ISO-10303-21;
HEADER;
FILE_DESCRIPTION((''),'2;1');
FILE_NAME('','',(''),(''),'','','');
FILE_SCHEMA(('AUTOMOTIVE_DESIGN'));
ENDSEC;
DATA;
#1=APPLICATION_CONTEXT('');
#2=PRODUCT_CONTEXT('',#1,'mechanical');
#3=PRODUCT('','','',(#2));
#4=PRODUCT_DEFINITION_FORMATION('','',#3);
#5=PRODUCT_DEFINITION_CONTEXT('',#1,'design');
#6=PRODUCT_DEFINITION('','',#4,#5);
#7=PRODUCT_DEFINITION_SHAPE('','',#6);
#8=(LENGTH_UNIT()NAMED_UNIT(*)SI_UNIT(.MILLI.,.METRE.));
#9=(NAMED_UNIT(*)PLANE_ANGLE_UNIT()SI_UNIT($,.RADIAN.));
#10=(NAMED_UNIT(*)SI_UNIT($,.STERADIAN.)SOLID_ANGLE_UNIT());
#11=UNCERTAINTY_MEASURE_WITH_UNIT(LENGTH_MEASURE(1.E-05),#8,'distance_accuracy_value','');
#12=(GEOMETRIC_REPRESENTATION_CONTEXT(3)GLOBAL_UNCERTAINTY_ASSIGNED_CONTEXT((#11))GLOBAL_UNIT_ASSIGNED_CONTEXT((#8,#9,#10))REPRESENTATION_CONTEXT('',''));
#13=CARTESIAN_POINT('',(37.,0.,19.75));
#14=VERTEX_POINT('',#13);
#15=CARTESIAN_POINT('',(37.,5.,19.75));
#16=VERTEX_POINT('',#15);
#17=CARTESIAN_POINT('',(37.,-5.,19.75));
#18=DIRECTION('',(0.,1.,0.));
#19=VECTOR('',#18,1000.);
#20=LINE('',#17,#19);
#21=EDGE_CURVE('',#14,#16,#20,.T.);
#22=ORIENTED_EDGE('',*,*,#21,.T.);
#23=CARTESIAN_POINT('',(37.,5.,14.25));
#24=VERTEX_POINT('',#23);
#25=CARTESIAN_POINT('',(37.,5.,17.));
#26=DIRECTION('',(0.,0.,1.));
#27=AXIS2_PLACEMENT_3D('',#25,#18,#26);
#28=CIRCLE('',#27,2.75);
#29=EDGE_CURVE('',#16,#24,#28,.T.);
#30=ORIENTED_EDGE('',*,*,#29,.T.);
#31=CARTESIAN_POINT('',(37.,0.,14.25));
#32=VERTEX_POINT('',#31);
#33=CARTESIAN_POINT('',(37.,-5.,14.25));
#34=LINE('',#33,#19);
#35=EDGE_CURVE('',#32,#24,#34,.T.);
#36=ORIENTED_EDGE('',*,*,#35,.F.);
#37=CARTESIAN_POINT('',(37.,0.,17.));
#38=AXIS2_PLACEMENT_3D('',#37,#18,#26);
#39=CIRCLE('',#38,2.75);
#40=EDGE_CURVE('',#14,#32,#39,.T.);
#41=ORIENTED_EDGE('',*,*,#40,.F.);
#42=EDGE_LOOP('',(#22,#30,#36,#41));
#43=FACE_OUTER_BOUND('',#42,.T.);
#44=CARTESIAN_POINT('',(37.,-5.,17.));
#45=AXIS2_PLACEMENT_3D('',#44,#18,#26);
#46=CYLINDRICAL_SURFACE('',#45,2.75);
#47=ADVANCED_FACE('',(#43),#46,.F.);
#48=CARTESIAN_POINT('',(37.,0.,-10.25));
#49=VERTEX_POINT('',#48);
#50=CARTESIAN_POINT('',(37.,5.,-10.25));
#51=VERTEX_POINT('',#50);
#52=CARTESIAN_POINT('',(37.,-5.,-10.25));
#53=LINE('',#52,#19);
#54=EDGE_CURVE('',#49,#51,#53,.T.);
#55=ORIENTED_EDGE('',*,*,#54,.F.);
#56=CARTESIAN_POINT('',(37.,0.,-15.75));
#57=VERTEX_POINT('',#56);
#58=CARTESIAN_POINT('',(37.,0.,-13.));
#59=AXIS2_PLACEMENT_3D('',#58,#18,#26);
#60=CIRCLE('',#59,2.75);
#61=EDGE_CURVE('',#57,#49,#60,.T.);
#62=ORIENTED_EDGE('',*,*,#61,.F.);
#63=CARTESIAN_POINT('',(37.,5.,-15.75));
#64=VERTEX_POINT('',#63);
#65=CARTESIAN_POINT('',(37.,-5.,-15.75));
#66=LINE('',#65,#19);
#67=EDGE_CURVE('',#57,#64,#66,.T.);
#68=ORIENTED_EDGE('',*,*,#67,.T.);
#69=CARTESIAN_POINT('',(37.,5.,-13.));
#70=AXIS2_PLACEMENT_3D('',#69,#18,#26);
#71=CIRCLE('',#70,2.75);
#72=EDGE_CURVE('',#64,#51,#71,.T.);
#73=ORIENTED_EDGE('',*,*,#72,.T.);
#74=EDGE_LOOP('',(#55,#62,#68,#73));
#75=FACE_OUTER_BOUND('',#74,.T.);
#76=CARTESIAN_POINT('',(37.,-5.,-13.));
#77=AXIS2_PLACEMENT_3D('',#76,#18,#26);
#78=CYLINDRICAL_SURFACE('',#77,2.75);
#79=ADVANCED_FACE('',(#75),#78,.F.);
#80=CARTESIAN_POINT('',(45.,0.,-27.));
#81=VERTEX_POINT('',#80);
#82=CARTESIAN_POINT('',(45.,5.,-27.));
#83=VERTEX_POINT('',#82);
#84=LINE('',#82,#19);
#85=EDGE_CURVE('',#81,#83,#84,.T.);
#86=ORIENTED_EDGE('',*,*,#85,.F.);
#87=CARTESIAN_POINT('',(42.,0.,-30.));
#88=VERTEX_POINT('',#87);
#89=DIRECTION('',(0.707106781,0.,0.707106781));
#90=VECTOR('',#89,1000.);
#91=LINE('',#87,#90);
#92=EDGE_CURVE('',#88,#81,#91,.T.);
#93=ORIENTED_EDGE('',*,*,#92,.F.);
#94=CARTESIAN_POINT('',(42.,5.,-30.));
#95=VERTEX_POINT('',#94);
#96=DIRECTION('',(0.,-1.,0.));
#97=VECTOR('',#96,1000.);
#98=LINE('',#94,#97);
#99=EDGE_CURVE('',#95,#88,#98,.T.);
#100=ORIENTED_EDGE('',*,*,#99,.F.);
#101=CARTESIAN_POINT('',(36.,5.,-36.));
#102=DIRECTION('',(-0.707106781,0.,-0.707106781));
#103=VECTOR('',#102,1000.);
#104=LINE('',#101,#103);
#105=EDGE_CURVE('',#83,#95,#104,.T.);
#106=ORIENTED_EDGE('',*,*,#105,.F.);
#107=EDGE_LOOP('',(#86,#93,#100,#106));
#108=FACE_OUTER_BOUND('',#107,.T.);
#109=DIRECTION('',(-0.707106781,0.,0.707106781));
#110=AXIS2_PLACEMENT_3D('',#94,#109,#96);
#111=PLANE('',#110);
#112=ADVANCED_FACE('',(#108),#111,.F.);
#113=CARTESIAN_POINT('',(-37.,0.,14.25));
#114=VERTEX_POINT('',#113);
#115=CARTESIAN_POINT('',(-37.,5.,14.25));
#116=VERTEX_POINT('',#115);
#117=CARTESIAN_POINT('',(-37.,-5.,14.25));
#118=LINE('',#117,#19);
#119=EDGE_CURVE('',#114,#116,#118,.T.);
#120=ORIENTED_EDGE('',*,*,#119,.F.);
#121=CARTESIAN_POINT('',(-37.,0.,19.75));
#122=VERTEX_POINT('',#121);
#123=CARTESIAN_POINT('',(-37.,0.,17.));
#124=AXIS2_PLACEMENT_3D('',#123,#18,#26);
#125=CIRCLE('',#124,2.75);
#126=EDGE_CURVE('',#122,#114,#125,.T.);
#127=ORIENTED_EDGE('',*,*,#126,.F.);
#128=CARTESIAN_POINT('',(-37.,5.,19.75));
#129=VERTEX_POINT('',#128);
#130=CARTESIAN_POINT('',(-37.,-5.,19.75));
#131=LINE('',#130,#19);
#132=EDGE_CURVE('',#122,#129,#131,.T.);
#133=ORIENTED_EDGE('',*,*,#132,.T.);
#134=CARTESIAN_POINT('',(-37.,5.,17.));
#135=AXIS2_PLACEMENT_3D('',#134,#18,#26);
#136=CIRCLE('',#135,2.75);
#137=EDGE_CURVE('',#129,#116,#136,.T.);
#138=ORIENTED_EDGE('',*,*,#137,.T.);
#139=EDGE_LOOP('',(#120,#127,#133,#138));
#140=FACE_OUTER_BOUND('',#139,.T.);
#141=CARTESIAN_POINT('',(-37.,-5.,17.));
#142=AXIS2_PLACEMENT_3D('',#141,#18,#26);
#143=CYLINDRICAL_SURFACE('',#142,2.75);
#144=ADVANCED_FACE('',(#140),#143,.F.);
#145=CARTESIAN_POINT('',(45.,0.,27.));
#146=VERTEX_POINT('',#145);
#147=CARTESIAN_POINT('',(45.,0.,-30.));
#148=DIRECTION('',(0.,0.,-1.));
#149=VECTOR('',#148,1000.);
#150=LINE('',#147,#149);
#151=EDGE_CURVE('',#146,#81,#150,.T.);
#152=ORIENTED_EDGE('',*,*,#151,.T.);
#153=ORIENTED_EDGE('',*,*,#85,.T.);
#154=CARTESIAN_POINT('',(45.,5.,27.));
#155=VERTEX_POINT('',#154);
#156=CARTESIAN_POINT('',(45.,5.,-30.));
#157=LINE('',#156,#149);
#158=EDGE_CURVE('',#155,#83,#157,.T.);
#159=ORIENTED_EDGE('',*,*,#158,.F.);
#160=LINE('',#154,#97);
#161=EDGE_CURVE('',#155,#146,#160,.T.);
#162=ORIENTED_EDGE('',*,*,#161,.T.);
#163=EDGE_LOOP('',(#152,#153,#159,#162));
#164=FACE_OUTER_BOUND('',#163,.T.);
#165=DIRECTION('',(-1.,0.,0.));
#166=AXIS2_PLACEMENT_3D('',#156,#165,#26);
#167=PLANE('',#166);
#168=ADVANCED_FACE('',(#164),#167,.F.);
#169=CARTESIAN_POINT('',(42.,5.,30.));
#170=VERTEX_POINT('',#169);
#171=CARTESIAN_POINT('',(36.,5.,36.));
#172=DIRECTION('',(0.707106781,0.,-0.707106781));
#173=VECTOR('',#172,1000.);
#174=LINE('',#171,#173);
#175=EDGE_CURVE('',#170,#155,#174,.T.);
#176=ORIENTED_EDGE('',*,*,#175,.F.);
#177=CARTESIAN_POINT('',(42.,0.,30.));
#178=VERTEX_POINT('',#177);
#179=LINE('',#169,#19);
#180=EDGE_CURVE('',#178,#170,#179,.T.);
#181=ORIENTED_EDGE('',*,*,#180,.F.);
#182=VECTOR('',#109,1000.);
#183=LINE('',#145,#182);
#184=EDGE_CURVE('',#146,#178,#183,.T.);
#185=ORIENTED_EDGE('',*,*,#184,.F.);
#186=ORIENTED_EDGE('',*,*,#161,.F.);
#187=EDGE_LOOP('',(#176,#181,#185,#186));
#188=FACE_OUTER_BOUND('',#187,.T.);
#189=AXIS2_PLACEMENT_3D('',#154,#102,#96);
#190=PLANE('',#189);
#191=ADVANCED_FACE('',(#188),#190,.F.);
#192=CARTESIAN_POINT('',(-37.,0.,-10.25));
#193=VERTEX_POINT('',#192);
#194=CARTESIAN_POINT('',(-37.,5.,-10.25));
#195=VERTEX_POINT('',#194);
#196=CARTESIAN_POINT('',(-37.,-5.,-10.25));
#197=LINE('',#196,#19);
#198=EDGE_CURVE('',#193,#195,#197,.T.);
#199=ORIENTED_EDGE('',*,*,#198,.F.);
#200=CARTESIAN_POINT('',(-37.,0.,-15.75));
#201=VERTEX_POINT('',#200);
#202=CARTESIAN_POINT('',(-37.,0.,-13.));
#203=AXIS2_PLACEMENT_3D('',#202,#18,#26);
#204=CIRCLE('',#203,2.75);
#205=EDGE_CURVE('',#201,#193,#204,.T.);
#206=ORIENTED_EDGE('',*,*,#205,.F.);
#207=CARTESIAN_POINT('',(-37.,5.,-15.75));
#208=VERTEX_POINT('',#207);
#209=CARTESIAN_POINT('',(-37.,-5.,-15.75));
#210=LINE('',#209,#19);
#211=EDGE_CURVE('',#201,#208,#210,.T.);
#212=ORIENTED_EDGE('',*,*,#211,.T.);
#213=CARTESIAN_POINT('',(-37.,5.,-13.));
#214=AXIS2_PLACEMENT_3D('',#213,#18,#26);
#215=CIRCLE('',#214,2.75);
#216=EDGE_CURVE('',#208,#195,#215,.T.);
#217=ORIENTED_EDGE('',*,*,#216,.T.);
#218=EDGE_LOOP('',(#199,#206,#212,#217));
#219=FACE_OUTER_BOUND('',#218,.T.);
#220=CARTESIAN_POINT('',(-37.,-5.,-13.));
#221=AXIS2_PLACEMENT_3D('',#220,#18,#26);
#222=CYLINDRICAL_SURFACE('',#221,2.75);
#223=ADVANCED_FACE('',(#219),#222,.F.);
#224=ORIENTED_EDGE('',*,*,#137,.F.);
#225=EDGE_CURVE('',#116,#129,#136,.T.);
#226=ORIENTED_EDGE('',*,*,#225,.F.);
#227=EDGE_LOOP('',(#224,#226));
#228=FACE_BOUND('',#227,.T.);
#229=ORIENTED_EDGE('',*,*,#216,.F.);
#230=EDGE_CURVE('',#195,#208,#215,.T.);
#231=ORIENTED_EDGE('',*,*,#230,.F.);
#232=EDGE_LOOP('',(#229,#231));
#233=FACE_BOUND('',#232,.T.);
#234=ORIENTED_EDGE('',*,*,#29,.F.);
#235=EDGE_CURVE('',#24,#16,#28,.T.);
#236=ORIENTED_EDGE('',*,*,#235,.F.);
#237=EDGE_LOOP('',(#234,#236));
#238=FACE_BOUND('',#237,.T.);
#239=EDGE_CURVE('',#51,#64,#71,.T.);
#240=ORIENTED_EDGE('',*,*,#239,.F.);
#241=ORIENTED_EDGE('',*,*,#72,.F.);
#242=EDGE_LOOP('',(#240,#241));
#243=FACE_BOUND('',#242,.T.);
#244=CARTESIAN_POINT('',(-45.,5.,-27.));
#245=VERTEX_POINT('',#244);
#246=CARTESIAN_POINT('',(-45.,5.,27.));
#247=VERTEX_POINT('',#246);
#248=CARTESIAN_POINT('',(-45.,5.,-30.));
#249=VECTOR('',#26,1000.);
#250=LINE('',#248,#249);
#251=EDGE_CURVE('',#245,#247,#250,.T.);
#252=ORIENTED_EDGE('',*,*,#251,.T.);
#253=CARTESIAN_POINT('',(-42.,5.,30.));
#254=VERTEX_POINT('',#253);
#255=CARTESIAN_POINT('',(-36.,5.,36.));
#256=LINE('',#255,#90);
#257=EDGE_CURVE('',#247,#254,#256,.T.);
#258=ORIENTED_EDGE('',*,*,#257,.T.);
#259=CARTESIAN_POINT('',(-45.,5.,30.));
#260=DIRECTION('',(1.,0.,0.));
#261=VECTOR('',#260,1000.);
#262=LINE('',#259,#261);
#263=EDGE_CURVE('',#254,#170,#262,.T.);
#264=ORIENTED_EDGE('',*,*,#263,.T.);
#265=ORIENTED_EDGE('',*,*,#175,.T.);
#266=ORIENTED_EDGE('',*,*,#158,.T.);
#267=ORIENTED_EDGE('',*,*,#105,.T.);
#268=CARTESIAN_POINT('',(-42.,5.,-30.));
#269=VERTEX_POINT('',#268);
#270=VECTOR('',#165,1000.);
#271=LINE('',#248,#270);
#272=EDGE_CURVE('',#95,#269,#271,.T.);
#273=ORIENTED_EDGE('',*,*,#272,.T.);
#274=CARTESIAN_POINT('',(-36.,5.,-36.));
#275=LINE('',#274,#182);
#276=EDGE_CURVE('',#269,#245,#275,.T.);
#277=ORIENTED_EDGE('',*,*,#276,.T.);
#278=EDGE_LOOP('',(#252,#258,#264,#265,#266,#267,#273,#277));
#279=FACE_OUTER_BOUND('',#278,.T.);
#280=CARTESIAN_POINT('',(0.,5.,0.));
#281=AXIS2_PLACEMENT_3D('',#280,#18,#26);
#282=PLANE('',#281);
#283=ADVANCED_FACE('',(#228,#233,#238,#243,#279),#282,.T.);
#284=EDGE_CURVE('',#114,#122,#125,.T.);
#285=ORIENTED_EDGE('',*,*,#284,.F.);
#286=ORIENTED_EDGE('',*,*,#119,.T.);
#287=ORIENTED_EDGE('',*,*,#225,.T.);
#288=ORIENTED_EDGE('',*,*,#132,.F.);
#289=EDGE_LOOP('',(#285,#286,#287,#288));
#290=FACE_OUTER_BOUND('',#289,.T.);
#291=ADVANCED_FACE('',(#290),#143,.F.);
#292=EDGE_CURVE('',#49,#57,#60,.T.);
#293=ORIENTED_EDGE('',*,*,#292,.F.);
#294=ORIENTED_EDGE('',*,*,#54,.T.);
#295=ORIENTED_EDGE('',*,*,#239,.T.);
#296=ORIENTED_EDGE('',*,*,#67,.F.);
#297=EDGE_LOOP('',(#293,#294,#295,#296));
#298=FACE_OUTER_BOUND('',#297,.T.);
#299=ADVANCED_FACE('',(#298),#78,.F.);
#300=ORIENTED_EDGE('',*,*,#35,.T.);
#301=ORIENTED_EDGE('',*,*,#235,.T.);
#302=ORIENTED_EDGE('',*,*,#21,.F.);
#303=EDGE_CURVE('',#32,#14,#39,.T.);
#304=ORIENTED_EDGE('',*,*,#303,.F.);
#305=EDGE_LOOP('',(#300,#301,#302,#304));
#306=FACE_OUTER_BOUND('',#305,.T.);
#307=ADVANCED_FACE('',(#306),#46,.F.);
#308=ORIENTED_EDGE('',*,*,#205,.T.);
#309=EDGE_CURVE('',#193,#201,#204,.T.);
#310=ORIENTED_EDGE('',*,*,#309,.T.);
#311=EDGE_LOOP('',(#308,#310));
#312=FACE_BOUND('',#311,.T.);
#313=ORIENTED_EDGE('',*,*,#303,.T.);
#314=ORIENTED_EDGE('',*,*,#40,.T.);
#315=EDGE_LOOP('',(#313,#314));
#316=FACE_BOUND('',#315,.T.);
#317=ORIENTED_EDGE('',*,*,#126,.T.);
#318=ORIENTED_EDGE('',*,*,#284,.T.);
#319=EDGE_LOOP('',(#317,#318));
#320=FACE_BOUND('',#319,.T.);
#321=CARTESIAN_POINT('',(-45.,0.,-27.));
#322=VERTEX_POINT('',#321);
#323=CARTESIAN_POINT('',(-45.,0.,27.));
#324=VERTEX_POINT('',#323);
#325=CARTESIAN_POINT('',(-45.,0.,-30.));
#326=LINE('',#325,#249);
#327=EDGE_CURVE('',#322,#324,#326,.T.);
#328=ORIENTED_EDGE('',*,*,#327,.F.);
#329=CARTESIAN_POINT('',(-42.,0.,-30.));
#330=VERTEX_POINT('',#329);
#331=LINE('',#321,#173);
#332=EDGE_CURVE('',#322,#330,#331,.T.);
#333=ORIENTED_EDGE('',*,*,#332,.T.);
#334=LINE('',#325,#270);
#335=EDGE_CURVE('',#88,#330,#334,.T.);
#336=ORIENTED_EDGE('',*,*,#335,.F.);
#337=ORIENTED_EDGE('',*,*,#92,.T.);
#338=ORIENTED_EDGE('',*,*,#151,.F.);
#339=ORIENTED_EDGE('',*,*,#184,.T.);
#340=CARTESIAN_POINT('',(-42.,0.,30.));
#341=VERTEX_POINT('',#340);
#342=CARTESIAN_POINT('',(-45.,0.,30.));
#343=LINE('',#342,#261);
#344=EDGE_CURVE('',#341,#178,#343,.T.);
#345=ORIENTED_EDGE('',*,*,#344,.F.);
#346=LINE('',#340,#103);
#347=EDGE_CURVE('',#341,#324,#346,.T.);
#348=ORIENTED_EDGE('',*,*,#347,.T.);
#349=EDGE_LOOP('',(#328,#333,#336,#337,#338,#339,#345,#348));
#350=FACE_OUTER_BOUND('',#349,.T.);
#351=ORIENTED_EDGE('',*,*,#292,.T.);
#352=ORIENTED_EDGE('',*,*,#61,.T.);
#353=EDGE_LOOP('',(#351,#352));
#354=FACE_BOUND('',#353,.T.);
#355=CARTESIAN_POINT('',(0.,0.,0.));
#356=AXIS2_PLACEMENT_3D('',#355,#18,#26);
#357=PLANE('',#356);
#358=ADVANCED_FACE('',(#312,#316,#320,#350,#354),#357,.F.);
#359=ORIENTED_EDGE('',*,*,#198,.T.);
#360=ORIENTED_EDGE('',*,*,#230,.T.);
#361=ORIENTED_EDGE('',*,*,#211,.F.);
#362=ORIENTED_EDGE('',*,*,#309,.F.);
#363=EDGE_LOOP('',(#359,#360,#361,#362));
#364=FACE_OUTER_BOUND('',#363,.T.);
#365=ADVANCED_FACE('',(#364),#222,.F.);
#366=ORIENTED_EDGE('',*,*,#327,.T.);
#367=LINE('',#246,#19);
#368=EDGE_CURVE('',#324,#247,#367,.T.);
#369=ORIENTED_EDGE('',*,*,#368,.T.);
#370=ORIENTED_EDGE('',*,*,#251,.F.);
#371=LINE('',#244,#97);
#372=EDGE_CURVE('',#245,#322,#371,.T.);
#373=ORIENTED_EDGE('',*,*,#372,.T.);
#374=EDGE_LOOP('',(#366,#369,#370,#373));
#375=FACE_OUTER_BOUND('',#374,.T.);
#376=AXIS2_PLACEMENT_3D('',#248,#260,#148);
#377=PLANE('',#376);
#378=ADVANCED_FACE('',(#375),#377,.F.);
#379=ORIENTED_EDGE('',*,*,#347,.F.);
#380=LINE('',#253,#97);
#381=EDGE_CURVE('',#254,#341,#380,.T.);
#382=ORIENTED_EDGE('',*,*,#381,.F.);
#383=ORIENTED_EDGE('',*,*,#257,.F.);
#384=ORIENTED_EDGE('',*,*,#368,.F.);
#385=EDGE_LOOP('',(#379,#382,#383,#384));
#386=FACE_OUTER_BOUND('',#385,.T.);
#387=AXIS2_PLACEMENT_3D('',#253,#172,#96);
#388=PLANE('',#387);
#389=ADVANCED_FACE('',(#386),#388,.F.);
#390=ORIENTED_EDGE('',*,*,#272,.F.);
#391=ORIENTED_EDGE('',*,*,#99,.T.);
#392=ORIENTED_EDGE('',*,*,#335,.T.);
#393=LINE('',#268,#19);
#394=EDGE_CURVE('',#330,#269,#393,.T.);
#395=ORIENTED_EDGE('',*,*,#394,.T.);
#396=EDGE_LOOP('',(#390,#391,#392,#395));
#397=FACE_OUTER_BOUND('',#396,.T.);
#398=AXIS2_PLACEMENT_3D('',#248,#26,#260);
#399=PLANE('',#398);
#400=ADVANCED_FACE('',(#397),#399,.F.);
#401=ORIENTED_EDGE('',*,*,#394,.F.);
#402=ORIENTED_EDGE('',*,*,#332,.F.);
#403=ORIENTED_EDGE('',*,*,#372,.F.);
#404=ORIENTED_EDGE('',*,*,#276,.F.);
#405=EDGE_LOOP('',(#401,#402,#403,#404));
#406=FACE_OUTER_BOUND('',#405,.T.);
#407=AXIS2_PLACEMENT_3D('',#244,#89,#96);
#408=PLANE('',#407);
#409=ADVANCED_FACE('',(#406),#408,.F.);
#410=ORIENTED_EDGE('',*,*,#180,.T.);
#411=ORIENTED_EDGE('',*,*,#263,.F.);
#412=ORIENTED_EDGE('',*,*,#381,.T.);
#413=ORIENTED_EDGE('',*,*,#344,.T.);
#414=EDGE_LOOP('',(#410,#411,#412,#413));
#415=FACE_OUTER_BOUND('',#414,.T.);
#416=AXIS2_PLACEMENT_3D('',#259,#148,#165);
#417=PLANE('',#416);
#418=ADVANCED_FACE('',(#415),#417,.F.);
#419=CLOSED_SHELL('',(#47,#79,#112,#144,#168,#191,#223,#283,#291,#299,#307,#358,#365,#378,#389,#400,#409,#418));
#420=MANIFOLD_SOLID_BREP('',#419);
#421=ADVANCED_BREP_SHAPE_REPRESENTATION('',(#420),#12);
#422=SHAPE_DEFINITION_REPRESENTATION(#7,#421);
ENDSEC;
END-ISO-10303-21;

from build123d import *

# Parameters (mm, degrees)
SKETCH_1_W          = 90
SKETCH_1_H          = 60
EXTRUDE_1_DEPTH     = 5
CHAMFER_1_SIZE      = 3
SKETCH_2_R          = 2.75
CUT_EXTRUDE_1_DEPTH = 10


with BuildPart() as part:
    # 草图1 → 凸台-拉伸1 (new body)
    with BuildSketch(Plane(origin=(0, 0, 0), x_dir=(1, 0, 0), z_dir=(0, 1, 0))):
        Rectangle(SKETCH_1_W, SKETCH_1_H)
    extrude(amount=EXTRUDE_1_DEPTH)

    # 倒角1
    chamfer_1_edges = [part.edges().sort_by_distance(p)[0] for p in [
        (45, 2.5, 30),
        (-45, 2.5, 30),
        (-45, 2.5, -30),
        (45, 2.5, -30),
    ]]
    chamfer(chamfer_1_edges, length=CHAMFER_1_SIZE)

    # 草图2 → 切除-拉伸1 (cut)
    with BuildSketch(Plane(origin=(0, 5, 0), x_dir=(1, 0, 0), z_dir=(0, 1, 0))):
        with Locations(Location((37, -17, 0), (0, 0, 270))):
            Circle(SKETCH_2_R)
        with Locations(Location((-37, -17, 0), (0, 0, 270))):
            Circle(SKETCH_2_R)
        with Locations(Location((37, 13, 0), (0, 0, 270))):
            Circle(SKETCH_2_R)
        with Locations(Location((-37, 13, 0), (0, 0, 270))):
            Circle(SKETCH_2_R)
    extrude(amount=-CUT_EXTRUDE_1_DEPTH, mode=Mode.SUBTRACT)


solid = part.part
